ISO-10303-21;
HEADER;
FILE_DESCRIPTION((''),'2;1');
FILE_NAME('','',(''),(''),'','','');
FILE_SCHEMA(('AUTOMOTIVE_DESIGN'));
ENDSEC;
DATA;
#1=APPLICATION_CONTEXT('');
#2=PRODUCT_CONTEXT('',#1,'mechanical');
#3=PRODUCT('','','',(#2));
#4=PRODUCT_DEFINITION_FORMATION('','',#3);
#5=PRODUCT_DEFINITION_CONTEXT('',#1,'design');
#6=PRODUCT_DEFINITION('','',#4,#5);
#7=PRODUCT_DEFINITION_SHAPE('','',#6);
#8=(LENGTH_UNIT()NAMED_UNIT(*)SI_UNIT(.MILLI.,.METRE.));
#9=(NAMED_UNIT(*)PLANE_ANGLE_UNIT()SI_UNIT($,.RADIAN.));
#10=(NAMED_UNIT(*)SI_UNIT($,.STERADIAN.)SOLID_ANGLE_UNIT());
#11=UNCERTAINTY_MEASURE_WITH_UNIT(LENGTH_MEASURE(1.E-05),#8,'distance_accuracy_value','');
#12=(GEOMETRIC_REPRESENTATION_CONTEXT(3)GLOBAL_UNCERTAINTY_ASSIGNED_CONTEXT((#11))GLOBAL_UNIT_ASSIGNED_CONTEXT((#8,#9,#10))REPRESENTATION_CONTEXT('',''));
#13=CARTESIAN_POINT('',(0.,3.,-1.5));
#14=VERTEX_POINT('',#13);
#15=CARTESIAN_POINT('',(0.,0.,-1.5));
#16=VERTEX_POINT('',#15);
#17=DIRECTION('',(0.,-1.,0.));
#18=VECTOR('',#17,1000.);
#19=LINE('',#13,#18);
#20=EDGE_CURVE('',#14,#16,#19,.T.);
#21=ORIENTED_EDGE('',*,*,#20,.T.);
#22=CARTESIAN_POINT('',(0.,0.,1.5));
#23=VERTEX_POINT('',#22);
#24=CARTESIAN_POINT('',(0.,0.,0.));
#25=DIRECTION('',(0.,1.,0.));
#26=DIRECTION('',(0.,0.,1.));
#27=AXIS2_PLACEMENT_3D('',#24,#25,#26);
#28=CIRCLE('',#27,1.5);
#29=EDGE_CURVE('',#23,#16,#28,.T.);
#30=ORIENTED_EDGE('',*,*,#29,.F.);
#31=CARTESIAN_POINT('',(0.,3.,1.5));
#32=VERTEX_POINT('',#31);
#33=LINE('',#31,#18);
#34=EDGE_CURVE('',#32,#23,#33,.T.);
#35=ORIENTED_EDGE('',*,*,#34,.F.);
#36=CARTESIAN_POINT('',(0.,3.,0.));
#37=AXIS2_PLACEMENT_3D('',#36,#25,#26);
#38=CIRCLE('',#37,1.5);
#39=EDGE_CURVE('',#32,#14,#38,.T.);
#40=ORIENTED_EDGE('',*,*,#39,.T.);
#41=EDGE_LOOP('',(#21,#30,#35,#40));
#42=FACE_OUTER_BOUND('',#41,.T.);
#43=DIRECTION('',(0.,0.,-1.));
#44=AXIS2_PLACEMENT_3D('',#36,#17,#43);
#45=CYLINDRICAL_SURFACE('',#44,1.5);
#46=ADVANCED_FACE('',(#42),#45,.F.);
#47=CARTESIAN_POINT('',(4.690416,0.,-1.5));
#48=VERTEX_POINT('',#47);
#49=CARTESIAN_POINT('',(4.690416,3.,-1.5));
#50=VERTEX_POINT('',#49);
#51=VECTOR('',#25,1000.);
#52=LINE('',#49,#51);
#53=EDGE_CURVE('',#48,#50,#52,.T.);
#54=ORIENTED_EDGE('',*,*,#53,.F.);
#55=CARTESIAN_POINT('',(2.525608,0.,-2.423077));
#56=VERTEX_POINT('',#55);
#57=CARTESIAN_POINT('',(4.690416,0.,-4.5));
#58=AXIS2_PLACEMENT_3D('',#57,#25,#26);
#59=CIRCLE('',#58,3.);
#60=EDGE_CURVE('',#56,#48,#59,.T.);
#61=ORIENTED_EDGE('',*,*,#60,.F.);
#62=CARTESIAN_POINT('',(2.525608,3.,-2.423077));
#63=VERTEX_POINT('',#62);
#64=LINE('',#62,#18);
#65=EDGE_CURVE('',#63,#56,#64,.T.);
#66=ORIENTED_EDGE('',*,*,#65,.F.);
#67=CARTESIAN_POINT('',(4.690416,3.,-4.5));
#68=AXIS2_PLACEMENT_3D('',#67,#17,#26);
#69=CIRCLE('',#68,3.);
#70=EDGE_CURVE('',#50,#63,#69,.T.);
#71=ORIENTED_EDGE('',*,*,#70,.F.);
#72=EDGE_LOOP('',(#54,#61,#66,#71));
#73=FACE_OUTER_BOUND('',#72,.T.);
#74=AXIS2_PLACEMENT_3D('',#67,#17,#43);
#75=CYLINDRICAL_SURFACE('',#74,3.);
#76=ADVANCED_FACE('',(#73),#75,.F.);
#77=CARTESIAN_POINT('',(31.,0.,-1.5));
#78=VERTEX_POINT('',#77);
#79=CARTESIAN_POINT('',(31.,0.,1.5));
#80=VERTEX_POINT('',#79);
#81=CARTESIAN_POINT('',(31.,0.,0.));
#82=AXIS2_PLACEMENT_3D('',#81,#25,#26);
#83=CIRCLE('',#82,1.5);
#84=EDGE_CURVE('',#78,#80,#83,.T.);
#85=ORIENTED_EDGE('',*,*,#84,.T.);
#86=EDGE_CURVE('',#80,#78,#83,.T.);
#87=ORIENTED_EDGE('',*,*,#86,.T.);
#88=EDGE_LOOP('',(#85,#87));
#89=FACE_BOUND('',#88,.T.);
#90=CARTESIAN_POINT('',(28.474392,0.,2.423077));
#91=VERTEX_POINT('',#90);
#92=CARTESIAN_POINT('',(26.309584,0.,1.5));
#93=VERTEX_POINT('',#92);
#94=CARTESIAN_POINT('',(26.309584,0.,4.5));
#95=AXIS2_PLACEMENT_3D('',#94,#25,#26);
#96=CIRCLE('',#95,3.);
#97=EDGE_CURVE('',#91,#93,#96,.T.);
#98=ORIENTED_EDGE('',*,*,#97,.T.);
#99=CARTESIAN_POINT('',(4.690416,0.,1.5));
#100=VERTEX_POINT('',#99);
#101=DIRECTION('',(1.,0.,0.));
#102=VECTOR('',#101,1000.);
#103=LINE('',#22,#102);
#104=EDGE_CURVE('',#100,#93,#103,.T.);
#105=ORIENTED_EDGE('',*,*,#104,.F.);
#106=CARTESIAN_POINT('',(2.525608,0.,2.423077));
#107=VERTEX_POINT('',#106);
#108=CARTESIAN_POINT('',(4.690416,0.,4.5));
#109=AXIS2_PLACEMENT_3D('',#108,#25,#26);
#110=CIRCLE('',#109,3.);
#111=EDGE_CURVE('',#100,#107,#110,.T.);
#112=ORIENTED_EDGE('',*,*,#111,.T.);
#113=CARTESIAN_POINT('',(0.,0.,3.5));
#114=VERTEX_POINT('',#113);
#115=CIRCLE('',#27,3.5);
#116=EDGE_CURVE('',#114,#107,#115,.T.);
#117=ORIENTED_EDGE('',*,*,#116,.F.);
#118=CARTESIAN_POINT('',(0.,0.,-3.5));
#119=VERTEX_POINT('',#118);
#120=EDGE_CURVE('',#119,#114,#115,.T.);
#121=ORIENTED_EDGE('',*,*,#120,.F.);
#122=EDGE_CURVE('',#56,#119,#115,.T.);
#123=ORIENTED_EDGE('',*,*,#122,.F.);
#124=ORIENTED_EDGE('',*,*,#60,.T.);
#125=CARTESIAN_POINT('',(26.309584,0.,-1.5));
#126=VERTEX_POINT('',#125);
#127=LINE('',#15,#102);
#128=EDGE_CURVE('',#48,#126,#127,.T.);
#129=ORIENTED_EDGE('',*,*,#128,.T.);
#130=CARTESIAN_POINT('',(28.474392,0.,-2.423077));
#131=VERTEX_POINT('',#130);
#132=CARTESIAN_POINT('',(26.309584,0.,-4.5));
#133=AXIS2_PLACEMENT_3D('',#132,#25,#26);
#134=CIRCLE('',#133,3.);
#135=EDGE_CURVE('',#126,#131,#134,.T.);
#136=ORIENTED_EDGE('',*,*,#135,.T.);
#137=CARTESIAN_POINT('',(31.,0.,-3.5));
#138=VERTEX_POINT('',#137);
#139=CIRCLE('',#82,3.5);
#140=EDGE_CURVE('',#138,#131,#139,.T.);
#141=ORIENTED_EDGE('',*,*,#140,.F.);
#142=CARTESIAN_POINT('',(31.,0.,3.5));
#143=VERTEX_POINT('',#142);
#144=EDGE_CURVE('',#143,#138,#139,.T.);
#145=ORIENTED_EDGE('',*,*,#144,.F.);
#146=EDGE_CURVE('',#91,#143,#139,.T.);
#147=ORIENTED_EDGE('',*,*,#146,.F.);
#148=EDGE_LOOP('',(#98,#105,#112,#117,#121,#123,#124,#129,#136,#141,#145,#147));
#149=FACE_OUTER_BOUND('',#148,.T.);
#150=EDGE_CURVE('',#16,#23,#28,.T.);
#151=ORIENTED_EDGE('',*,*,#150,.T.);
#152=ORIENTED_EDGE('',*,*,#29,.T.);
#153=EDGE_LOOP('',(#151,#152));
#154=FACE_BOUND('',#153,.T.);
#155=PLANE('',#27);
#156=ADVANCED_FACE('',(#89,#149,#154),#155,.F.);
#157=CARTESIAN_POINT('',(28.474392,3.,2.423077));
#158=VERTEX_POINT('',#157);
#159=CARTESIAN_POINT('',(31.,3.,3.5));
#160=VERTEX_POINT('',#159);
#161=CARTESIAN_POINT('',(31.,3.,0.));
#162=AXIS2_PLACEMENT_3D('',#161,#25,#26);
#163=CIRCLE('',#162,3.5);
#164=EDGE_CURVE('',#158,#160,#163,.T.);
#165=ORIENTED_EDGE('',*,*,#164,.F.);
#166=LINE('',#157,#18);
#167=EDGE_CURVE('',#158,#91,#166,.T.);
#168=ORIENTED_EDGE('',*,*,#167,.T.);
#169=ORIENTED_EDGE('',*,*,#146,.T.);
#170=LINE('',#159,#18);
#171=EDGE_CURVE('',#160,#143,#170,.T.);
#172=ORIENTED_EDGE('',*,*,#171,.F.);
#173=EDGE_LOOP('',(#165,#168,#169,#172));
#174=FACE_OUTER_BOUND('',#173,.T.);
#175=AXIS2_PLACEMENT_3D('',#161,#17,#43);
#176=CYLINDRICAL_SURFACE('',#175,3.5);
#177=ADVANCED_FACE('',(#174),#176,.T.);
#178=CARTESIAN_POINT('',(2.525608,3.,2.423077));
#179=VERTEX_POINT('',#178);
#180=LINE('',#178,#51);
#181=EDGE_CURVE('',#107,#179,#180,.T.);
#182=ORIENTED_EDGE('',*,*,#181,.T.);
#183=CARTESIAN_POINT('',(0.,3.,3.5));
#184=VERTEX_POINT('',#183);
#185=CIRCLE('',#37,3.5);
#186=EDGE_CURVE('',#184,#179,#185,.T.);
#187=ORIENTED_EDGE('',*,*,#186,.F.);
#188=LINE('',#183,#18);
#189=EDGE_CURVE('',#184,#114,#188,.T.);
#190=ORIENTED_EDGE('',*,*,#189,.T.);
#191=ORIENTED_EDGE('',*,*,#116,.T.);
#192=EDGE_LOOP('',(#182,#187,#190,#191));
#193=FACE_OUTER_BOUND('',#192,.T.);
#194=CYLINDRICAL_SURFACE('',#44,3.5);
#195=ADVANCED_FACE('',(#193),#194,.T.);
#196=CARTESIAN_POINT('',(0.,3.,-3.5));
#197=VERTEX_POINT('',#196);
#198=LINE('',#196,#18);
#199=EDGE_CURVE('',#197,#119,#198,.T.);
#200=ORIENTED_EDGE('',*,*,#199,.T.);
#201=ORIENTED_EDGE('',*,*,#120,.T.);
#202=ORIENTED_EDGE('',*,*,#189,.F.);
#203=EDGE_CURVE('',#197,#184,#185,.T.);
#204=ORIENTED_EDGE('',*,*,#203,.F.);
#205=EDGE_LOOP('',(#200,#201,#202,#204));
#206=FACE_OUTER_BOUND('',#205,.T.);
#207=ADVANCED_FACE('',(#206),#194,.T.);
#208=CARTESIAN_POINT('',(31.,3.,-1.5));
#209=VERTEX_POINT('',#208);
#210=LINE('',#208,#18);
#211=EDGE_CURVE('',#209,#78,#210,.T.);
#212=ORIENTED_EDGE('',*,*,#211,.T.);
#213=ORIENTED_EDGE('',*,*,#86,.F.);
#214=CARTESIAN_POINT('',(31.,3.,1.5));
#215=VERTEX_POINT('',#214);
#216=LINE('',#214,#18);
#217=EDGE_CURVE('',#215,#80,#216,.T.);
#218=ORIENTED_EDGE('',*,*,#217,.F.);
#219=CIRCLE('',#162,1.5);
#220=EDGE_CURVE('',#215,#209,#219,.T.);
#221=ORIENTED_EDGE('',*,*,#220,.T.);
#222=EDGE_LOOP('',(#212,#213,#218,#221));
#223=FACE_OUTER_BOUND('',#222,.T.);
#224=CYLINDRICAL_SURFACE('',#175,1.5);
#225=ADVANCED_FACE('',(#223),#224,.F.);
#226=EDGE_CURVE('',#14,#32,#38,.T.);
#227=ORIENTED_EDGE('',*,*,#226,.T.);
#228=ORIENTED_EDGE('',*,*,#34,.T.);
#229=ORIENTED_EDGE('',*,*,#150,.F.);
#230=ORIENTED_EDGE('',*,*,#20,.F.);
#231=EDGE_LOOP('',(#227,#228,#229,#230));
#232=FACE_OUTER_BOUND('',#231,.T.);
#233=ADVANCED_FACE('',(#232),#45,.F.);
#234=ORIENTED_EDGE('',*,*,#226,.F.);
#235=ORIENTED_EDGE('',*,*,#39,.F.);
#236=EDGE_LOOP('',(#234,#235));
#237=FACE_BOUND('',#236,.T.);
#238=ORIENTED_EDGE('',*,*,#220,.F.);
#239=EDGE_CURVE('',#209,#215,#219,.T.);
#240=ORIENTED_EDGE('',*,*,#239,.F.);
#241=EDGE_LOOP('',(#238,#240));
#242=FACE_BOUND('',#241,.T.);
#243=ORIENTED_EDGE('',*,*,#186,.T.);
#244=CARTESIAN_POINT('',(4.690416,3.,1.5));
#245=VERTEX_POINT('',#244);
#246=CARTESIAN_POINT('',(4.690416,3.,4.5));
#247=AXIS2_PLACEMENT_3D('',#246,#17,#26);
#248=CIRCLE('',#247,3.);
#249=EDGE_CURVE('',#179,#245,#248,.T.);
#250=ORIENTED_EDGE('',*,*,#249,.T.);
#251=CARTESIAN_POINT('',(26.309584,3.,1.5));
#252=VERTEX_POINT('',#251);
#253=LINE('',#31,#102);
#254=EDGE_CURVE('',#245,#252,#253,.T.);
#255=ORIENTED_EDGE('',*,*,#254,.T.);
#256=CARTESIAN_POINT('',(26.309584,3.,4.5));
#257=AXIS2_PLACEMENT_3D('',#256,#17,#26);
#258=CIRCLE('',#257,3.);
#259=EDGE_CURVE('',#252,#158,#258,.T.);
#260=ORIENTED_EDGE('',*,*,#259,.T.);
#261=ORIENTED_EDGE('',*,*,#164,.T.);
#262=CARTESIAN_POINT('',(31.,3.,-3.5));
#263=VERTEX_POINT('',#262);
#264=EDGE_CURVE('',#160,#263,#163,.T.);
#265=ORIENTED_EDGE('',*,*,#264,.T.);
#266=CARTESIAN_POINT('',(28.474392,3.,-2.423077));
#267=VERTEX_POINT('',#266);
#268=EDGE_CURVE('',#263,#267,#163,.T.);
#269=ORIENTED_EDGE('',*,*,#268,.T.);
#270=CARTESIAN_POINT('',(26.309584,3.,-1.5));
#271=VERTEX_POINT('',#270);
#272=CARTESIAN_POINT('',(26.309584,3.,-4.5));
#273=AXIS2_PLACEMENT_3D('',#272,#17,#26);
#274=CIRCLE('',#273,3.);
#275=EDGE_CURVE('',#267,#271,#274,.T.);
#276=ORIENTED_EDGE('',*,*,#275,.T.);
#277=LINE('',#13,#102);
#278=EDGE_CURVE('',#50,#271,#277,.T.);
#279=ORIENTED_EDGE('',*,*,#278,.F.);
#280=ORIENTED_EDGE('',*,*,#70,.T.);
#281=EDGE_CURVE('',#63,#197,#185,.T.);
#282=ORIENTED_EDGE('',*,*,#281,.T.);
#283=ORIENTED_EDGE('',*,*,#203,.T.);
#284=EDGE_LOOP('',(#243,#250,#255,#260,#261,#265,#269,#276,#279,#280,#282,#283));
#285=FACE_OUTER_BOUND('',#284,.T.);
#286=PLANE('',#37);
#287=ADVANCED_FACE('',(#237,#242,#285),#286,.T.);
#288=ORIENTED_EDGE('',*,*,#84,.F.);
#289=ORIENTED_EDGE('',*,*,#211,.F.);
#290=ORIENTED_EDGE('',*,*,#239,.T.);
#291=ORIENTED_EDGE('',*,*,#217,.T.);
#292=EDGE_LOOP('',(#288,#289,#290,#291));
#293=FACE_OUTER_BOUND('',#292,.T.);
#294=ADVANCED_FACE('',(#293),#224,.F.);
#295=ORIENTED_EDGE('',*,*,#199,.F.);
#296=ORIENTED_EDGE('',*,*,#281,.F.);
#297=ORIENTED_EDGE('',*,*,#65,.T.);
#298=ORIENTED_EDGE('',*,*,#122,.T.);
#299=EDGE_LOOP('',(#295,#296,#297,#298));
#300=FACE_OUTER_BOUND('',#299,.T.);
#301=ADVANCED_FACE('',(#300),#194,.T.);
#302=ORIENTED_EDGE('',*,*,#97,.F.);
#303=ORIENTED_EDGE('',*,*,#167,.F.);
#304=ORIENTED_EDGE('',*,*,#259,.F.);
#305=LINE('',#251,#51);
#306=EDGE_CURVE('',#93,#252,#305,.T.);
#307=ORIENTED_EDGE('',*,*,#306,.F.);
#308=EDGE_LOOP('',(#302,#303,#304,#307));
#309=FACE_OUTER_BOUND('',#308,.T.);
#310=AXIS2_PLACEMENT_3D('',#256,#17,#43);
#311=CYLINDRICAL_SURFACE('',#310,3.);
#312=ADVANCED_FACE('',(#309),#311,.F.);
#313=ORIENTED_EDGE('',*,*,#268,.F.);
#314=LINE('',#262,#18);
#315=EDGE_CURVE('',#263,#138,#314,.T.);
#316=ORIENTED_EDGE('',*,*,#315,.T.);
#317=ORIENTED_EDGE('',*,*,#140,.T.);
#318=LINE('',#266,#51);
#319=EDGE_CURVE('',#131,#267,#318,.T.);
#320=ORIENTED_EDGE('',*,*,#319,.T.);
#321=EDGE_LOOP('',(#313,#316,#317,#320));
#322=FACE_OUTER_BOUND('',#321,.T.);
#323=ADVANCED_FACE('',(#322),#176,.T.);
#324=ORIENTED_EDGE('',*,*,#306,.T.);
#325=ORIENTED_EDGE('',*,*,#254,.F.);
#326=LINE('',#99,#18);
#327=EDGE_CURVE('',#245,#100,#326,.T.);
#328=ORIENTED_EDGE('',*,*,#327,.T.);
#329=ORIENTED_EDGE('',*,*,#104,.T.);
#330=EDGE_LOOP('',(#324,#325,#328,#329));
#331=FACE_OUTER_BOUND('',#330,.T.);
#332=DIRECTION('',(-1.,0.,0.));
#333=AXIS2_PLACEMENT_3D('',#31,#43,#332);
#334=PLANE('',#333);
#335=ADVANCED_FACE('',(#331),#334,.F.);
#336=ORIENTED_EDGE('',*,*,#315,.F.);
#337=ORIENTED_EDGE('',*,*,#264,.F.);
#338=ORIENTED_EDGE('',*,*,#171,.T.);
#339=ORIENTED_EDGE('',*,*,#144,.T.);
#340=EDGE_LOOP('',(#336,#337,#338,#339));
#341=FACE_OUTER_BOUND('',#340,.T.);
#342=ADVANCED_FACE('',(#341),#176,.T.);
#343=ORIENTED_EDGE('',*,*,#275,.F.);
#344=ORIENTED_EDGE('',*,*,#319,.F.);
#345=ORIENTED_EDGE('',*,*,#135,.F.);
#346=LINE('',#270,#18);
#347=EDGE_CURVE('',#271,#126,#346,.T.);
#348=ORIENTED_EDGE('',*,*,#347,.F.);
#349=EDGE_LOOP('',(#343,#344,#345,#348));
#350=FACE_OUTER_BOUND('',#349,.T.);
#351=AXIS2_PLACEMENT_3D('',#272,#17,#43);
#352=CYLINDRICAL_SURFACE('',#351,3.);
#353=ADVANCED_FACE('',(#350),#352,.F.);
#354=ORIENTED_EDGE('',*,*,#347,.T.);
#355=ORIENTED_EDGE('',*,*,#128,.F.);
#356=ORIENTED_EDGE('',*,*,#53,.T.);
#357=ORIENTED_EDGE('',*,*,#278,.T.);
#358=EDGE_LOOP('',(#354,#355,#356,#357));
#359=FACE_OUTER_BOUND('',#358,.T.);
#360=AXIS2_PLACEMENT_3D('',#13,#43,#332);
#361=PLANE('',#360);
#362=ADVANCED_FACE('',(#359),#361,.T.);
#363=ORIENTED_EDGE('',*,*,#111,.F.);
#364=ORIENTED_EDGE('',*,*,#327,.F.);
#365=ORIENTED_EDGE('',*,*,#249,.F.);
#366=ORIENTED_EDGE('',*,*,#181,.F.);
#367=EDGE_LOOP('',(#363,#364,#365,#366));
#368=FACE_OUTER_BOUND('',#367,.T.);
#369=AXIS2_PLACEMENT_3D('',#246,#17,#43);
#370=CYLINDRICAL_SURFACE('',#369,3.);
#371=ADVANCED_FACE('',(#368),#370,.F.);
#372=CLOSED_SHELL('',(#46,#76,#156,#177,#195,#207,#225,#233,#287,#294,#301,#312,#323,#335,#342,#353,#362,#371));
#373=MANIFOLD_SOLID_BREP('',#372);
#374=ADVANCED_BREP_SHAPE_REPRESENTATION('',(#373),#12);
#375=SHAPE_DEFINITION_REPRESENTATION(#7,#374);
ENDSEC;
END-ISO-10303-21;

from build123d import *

# Parameters (mm, degrees)
SKETCH1_R           = 1.5
BOSS_EXTRUDE1_DEPTH = 3
FILLET1_R           = 3


with BuildPart() as part:
    # Sketch1 → Boss-Extrude1 (new body)
    with BuildSketch(Plane(origin=(0, 0, 0), x_dir=(1, 0, 0), z_dir=(0, 1, 0))):
        with BuildLine():
            ThreePointArc((3.16227766, 1.5), (-3.5, 0), (3.16227766, -1.5))
            Line((3.16227766, -1.5), (27.83772234, -1.5))
            ThreePointArc((27.83772234, -1.5), (34.5, 0), (27.83772234, 1.5))
            Line((27.83772234, 1.5), (3.16227766, 1.5))
        make_face()
        with Locations(Location((0, 0, 0), (0, 0, 270))):
            Circle(SKETCH1_R, mode=Mode.SUBTRACT)
        with Locations(Location((31, 0, 0), (0, 0, 270))):
            Circle(SKETCH1_R, mode=Mode.SUBTRACT)
    extrude(amount=BOSS_EXTRUDE1_DEPTH)

    # Fillet1
    fillet1_edges = [part.edges().sort_by_distance(p)[0] for p in [
        (27.83772234, 1.5, 1.5),
        (3.16227766, 1.5, 1.5),
        (3.16227766, 1.5, -1.5),
        (27.83772234, 1.5, -1.5),
    ]]
    fillet(fillet1_edges, radius=FILLET1_R)


solid = part.part
